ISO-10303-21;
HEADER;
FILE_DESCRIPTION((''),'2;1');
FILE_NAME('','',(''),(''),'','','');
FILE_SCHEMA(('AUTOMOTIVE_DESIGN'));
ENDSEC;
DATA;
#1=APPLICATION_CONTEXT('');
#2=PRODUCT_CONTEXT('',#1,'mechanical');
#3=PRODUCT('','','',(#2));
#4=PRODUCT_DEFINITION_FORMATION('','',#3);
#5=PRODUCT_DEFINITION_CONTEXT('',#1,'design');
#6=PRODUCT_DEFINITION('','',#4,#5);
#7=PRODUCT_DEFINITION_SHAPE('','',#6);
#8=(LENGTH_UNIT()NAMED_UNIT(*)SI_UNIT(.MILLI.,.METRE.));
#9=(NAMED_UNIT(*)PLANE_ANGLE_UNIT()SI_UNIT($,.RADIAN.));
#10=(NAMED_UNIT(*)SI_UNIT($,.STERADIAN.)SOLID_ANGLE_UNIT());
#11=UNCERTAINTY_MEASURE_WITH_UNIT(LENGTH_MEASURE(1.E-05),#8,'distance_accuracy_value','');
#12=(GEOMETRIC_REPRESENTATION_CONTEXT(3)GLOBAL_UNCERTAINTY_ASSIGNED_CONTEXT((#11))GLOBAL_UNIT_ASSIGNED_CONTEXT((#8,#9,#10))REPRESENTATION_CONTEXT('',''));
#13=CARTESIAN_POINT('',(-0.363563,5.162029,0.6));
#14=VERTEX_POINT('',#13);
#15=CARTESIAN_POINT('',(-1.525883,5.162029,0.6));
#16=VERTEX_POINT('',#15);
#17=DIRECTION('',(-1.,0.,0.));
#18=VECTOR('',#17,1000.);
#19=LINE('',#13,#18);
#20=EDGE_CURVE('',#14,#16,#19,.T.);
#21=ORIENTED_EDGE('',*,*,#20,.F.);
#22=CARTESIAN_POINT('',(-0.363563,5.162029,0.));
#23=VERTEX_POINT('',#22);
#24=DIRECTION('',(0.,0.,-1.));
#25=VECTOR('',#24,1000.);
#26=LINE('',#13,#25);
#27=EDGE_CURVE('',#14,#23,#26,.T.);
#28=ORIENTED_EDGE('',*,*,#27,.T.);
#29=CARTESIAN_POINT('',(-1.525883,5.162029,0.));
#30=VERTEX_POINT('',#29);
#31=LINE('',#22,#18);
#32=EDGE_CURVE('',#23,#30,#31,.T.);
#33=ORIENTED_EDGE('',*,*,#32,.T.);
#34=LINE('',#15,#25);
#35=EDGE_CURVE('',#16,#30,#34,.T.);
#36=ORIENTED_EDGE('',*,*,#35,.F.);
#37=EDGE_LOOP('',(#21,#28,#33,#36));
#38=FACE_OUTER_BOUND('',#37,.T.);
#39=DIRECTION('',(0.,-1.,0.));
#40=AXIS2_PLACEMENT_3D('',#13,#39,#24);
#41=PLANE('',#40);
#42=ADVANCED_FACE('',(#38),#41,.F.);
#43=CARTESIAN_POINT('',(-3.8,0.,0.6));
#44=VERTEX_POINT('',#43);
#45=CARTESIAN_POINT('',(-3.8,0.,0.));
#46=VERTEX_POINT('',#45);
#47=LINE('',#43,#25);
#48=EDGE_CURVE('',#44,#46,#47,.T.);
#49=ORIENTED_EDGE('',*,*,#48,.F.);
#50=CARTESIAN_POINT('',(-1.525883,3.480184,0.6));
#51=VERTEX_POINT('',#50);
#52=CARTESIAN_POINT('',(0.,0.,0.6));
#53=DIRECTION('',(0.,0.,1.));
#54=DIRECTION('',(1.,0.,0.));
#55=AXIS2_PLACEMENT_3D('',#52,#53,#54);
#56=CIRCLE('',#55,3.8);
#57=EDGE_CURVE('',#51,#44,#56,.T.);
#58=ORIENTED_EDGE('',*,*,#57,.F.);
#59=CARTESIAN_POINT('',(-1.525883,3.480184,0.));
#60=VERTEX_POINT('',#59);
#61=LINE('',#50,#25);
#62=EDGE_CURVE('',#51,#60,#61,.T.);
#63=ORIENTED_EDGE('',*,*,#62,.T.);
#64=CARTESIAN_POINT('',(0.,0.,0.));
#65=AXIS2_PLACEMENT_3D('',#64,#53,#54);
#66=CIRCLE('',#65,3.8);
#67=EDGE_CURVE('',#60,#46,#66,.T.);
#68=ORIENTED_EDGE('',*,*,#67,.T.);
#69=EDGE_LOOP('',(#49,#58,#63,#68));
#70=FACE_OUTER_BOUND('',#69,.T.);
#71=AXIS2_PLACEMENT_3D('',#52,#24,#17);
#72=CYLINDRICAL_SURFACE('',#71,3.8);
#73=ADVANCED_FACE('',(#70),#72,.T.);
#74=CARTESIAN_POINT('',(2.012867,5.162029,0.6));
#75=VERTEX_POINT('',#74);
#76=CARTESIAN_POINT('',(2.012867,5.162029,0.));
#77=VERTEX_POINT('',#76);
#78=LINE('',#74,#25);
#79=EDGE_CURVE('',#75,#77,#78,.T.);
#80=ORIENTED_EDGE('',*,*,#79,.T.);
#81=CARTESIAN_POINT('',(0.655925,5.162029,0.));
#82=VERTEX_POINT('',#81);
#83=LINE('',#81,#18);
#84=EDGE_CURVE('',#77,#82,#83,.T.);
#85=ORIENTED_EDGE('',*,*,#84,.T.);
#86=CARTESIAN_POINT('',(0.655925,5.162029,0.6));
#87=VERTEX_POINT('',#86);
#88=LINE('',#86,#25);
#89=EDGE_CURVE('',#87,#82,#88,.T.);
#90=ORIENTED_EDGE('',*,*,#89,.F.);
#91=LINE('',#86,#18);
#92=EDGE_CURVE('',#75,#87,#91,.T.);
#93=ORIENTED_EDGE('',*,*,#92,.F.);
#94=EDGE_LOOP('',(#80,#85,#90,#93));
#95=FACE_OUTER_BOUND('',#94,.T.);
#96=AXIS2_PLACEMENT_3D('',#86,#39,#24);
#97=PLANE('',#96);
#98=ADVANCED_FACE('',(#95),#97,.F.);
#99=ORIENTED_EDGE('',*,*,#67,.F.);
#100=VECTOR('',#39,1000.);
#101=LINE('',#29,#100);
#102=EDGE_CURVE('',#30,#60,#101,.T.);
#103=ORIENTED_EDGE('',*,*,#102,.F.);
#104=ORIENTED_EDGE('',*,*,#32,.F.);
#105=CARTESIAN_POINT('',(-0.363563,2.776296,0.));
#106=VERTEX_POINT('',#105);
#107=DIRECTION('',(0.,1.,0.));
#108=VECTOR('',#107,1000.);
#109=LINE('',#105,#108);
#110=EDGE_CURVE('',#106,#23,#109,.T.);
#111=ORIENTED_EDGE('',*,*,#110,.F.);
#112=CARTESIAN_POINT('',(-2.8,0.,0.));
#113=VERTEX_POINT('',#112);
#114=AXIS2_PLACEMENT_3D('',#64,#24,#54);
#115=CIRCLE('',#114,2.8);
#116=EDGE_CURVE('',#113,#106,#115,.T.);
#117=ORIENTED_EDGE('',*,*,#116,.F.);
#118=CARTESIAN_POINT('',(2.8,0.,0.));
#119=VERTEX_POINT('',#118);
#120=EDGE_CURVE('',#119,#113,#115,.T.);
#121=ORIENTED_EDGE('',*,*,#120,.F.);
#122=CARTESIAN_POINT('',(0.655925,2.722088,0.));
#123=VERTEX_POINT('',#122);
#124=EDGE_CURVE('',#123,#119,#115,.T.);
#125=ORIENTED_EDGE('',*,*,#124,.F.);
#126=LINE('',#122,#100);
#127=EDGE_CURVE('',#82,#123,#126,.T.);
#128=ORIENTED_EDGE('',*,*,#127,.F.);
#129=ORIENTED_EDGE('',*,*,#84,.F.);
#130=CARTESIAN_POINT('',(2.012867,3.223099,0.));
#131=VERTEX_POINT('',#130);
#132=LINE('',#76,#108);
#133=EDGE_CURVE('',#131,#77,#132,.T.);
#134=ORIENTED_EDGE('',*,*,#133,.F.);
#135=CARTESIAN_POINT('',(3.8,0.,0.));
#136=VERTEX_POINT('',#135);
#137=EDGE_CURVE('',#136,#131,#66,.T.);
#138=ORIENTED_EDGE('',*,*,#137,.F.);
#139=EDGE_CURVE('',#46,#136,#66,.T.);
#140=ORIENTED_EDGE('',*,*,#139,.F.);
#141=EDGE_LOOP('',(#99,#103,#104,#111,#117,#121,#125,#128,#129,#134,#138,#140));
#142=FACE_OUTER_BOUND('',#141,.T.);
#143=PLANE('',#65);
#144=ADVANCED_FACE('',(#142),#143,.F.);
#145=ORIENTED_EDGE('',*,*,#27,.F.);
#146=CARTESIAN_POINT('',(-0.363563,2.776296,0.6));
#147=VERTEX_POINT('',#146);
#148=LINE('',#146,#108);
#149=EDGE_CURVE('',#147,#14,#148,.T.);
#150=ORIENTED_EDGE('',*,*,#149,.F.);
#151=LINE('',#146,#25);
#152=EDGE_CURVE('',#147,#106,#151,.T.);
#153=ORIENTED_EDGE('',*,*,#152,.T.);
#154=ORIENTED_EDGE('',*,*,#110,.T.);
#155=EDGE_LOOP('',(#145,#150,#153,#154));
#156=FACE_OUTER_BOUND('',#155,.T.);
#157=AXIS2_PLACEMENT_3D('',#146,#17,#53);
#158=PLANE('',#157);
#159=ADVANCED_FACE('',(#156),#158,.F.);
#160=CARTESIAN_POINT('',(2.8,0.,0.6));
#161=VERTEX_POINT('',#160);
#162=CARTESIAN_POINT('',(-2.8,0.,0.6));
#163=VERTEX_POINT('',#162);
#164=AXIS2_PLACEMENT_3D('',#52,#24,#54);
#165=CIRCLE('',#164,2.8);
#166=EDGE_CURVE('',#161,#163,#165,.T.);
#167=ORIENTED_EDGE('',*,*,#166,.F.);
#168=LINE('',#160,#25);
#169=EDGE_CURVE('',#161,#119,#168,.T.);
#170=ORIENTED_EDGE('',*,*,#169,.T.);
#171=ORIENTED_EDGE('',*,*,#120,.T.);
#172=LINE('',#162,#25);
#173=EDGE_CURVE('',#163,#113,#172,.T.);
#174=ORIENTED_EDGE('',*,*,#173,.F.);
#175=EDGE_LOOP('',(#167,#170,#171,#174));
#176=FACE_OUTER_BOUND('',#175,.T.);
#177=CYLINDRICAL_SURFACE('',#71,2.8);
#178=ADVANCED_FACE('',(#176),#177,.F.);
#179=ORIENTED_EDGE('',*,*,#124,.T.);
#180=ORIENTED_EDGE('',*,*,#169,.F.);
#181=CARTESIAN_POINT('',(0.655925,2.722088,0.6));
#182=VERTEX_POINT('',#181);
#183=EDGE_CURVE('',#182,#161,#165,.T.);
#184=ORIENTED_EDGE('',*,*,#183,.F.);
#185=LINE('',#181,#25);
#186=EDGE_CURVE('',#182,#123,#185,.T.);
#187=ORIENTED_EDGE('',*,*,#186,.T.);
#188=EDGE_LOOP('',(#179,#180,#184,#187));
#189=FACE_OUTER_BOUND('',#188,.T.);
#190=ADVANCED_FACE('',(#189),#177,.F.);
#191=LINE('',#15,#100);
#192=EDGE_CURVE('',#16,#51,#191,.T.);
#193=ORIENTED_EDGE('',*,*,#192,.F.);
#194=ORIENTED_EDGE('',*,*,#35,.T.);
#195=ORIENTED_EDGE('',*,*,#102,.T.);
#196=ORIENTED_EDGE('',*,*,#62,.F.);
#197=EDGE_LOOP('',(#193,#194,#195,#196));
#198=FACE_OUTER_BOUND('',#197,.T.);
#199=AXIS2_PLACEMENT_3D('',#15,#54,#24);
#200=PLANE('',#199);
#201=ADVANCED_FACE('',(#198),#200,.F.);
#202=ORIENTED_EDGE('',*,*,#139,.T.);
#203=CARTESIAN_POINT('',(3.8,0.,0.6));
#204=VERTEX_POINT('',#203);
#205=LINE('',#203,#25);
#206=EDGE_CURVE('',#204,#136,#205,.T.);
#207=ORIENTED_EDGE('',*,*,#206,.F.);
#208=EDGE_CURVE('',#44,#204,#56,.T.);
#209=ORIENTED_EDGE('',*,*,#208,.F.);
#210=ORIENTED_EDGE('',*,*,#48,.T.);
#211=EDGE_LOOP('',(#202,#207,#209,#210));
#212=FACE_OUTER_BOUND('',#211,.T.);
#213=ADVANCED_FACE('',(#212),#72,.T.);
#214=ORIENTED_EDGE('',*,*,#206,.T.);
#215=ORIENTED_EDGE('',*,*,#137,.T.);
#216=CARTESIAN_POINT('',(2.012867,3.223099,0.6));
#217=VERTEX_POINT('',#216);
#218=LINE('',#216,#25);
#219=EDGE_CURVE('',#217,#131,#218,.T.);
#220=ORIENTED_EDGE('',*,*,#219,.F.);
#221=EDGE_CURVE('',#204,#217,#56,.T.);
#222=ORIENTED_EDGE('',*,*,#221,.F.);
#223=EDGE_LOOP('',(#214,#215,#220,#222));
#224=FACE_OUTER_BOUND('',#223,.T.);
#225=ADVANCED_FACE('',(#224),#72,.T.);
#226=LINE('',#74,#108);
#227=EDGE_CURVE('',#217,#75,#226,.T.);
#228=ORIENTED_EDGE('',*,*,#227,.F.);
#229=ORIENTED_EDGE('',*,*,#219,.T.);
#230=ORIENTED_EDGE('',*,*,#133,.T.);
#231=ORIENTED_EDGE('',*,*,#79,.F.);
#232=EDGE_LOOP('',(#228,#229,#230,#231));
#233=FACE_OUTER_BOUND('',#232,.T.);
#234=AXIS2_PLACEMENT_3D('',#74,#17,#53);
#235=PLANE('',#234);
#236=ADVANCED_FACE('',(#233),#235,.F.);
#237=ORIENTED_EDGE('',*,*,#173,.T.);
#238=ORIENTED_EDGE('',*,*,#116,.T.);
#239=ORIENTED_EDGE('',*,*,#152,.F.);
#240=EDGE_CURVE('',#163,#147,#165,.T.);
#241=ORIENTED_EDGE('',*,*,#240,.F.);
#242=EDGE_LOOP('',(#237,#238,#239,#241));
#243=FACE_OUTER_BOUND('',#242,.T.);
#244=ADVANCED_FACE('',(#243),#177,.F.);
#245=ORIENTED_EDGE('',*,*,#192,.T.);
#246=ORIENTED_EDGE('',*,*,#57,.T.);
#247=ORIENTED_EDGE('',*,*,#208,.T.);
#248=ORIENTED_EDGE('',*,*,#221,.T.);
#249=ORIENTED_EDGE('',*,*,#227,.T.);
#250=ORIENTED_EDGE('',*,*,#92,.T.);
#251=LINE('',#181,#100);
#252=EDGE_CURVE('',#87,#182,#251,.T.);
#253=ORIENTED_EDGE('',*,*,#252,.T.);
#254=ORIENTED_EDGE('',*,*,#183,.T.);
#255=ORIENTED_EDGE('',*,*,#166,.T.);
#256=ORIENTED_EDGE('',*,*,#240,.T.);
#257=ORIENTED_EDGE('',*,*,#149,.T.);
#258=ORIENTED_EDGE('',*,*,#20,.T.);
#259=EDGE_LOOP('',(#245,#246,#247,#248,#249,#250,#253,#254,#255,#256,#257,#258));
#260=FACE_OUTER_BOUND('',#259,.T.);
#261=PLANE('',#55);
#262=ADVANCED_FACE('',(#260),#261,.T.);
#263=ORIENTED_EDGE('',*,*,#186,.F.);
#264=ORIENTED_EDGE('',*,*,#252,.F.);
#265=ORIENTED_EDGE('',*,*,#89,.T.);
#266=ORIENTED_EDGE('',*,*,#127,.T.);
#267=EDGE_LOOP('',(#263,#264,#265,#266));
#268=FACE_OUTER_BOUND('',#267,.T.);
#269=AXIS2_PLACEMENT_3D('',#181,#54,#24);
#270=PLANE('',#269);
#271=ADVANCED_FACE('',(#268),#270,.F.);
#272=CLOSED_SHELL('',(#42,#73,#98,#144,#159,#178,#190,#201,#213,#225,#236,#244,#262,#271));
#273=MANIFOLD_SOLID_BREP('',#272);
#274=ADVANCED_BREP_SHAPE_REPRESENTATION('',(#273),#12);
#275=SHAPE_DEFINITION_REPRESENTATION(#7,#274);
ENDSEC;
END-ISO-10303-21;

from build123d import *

# Parameters (mm, degrees)
BOSS_EXTRUDE1_DEPTH = 0.6


with BuildPart() as part:
    # Sketch1 → Boss-Extrude1 (new body)
    with BuildSketch(Plane.XY):
        with BuildLine():
            Line((0.655924801, 2.722087922), (0.655924801, 5.162028968))
            Line((0.655924801, 5.162028968), (2.012866642, 5.162028968))
            Line((2.012866642, 5.162028968), (2.012866642, 3.223099112))
            ThreePointArc((2.012866642, 3.223099112), (-0.275338884, -3.790011675), (-1.525882777, 3.480184155))
            Line((-1.525882777, 3.480184155), (-1.525882777, 5.162028968))
            Line((-1.525882777, 5.162028968), (-0.363562636, 5.162028968))
            Line((-0.363562636, 5.162028968), (-0.363562636, 2.776296492))
            ThreePointArc((-0.363562636, 2.776296492), (-0.148672631, -2.796050151), (0.655924801, 2.722087922))
        make_face()
    extrude(amount=BOSS_EXTRUDE1_DEPTH)


solid = part.part
